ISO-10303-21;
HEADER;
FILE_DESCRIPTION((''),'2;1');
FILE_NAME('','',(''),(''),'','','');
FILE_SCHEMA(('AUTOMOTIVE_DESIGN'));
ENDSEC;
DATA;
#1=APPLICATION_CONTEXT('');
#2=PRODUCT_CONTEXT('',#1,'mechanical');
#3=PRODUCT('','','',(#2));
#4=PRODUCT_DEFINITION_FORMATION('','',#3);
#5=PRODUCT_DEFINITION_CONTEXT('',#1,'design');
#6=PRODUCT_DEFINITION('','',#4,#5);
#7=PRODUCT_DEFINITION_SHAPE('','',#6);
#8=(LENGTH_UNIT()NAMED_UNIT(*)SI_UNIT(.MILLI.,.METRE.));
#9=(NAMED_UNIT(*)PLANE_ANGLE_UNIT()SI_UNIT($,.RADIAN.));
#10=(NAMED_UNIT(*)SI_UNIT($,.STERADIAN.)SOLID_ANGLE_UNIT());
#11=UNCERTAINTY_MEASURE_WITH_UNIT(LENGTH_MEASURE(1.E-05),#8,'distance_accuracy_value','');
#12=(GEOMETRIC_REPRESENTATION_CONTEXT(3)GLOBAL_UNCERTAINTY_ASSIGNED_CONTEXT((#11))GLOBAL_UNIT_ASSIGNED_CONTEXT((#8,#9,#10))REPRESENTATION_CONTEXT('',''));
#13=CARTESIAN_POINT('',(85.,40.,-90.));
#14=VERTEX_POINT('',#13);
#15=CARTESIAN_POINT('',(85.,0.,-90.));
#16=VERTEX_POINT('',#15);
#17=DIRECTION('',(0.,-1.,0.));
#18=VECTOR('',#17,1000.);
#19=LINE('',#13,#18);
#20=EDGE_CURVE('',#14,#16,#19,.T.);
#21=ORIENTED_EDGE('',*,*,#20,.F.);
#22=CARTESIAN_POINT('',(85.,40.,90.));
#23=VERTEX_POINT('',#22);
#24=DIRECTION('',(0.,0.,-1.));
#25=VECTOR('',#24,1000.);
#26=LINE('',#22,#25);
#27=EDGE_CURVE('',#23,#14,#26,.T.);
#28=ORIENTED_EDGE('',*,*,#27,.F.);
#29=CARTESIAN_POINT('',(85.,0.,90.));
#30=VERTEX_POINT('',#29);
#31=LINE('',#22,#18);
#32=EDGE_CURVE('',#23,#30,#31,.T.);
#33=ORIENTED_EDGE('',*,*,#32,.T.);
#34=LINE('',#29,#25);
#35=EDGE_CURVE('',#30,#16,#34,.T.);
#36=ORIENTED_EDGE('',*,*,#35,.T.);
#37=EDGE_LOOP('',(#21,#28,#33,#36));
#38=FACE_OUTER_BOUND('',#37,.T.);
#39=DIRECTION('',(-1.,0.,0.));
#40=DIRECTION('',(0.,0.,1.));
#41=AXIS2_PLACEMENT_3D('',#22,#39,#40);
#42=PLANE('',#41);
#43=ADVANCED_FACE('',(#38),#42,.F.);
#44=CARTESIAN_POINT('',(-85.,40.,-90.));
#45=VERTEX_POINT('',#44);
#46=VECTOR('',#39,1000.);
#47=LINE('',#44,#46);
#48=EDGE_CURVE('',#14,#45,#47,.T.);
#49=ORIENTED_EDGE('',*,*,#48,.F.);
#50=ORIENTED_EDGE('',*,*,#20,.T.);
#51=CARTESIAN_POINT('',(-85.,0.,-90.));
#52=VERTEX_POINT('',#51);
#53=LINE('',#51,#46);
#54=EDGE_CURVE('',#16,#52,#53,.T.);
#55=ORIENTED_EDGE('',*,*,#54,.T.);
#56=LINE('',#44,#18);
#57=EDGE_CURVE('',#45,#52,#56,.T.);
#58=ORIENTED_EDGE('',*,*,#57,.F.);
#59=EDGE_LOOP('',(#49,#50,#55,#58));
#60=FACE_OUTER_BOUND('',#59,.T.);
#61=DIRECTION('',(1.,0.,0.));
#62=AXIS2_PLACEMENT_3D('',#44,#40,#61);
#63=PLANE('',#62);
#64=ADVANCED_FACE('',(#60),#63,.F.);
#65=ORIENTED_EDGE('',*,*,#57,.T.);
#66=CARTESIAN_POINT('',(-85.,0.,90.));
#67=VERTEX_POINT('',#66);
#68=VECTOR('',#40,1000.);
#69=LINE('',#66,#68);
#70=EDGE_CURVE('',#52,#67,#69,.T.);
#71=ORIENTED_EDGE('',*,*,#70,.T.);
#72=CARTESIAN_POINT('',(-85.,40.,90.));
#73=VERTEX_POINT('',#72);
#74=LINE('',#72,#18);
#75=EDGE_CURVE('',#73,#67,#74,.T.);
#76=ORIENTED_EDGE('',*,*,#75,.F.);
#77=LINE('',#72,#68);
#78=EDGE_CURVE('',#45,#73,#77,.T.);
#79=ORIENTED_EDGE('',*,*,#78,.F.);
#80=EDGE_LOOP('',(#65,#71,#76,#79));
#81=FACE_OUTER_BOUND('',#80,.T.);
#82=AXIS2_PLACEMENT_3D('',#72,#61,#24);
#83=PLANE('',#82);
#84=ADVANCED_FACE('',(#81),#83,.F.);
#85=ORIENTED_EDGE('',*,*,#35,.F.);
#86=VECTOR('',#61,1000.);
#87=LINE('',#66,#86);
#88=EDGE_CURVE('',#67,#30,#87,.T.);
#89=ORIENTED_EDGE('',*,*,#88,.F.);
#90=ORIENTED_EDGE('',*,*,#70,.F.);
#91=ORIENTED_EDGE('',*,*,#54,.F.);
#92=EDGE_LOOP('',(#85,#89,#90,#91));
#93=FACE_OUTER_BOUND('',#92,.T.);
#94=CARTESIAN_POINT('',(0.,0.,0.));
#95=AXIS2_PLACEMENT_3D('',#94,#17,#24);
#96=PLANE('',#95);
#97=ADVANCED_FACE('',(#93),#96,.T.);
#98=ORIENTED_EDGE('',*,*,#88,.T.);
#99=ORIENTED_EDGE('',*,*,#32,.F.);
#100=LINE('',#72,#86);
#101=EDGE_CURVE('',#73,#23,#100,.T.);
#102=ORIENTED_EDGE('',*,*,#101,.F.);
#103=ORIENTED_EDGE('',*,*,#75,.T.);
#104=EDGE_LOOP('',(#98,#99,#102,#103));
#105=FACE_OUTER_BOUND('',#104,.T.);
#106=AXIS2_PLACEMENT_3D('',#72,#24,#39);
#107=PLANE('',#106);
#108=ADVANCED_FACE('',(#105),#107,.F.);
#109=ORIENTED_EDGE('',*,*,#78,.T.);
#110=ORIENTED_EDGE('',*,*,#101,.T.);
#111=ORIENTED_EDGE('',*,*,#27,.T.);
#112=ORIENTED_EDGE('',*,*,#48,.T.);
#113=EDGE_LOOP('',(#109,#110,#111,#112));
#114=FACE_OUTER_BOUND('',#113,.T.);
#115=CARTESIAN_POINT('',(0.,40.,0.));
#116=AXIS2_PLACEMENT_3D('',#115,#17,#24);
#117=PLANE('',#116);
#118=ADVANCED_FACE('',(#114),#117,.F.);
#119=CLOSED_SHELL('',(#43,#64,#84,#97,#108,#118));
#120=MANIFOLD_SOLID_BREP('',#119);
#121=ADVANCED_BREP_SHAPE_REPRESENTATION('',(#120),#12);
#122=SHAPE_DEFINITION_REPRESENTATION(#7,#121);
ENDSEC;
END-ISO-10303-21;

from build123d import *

# Parameters (mm, degrees)
SKETCH_1_W      = 170
SKETCH_1_H      = 180
EXTRUDE_1_DEPTH = 40


with BuildPart() as part:
    # 草图1 → 凸台-拉伸1 (new body)
    with BuildSketch(Plane(origin=(0, 0, 0), x_dir=(1, 0, 0), z_dir=(0, 1, 0))):
        Rectangle(SKETCH_1_W, SKETCH_1_H)
    extrude(amount=EXTRUDE_1_DEPTH)


solid = part.part
